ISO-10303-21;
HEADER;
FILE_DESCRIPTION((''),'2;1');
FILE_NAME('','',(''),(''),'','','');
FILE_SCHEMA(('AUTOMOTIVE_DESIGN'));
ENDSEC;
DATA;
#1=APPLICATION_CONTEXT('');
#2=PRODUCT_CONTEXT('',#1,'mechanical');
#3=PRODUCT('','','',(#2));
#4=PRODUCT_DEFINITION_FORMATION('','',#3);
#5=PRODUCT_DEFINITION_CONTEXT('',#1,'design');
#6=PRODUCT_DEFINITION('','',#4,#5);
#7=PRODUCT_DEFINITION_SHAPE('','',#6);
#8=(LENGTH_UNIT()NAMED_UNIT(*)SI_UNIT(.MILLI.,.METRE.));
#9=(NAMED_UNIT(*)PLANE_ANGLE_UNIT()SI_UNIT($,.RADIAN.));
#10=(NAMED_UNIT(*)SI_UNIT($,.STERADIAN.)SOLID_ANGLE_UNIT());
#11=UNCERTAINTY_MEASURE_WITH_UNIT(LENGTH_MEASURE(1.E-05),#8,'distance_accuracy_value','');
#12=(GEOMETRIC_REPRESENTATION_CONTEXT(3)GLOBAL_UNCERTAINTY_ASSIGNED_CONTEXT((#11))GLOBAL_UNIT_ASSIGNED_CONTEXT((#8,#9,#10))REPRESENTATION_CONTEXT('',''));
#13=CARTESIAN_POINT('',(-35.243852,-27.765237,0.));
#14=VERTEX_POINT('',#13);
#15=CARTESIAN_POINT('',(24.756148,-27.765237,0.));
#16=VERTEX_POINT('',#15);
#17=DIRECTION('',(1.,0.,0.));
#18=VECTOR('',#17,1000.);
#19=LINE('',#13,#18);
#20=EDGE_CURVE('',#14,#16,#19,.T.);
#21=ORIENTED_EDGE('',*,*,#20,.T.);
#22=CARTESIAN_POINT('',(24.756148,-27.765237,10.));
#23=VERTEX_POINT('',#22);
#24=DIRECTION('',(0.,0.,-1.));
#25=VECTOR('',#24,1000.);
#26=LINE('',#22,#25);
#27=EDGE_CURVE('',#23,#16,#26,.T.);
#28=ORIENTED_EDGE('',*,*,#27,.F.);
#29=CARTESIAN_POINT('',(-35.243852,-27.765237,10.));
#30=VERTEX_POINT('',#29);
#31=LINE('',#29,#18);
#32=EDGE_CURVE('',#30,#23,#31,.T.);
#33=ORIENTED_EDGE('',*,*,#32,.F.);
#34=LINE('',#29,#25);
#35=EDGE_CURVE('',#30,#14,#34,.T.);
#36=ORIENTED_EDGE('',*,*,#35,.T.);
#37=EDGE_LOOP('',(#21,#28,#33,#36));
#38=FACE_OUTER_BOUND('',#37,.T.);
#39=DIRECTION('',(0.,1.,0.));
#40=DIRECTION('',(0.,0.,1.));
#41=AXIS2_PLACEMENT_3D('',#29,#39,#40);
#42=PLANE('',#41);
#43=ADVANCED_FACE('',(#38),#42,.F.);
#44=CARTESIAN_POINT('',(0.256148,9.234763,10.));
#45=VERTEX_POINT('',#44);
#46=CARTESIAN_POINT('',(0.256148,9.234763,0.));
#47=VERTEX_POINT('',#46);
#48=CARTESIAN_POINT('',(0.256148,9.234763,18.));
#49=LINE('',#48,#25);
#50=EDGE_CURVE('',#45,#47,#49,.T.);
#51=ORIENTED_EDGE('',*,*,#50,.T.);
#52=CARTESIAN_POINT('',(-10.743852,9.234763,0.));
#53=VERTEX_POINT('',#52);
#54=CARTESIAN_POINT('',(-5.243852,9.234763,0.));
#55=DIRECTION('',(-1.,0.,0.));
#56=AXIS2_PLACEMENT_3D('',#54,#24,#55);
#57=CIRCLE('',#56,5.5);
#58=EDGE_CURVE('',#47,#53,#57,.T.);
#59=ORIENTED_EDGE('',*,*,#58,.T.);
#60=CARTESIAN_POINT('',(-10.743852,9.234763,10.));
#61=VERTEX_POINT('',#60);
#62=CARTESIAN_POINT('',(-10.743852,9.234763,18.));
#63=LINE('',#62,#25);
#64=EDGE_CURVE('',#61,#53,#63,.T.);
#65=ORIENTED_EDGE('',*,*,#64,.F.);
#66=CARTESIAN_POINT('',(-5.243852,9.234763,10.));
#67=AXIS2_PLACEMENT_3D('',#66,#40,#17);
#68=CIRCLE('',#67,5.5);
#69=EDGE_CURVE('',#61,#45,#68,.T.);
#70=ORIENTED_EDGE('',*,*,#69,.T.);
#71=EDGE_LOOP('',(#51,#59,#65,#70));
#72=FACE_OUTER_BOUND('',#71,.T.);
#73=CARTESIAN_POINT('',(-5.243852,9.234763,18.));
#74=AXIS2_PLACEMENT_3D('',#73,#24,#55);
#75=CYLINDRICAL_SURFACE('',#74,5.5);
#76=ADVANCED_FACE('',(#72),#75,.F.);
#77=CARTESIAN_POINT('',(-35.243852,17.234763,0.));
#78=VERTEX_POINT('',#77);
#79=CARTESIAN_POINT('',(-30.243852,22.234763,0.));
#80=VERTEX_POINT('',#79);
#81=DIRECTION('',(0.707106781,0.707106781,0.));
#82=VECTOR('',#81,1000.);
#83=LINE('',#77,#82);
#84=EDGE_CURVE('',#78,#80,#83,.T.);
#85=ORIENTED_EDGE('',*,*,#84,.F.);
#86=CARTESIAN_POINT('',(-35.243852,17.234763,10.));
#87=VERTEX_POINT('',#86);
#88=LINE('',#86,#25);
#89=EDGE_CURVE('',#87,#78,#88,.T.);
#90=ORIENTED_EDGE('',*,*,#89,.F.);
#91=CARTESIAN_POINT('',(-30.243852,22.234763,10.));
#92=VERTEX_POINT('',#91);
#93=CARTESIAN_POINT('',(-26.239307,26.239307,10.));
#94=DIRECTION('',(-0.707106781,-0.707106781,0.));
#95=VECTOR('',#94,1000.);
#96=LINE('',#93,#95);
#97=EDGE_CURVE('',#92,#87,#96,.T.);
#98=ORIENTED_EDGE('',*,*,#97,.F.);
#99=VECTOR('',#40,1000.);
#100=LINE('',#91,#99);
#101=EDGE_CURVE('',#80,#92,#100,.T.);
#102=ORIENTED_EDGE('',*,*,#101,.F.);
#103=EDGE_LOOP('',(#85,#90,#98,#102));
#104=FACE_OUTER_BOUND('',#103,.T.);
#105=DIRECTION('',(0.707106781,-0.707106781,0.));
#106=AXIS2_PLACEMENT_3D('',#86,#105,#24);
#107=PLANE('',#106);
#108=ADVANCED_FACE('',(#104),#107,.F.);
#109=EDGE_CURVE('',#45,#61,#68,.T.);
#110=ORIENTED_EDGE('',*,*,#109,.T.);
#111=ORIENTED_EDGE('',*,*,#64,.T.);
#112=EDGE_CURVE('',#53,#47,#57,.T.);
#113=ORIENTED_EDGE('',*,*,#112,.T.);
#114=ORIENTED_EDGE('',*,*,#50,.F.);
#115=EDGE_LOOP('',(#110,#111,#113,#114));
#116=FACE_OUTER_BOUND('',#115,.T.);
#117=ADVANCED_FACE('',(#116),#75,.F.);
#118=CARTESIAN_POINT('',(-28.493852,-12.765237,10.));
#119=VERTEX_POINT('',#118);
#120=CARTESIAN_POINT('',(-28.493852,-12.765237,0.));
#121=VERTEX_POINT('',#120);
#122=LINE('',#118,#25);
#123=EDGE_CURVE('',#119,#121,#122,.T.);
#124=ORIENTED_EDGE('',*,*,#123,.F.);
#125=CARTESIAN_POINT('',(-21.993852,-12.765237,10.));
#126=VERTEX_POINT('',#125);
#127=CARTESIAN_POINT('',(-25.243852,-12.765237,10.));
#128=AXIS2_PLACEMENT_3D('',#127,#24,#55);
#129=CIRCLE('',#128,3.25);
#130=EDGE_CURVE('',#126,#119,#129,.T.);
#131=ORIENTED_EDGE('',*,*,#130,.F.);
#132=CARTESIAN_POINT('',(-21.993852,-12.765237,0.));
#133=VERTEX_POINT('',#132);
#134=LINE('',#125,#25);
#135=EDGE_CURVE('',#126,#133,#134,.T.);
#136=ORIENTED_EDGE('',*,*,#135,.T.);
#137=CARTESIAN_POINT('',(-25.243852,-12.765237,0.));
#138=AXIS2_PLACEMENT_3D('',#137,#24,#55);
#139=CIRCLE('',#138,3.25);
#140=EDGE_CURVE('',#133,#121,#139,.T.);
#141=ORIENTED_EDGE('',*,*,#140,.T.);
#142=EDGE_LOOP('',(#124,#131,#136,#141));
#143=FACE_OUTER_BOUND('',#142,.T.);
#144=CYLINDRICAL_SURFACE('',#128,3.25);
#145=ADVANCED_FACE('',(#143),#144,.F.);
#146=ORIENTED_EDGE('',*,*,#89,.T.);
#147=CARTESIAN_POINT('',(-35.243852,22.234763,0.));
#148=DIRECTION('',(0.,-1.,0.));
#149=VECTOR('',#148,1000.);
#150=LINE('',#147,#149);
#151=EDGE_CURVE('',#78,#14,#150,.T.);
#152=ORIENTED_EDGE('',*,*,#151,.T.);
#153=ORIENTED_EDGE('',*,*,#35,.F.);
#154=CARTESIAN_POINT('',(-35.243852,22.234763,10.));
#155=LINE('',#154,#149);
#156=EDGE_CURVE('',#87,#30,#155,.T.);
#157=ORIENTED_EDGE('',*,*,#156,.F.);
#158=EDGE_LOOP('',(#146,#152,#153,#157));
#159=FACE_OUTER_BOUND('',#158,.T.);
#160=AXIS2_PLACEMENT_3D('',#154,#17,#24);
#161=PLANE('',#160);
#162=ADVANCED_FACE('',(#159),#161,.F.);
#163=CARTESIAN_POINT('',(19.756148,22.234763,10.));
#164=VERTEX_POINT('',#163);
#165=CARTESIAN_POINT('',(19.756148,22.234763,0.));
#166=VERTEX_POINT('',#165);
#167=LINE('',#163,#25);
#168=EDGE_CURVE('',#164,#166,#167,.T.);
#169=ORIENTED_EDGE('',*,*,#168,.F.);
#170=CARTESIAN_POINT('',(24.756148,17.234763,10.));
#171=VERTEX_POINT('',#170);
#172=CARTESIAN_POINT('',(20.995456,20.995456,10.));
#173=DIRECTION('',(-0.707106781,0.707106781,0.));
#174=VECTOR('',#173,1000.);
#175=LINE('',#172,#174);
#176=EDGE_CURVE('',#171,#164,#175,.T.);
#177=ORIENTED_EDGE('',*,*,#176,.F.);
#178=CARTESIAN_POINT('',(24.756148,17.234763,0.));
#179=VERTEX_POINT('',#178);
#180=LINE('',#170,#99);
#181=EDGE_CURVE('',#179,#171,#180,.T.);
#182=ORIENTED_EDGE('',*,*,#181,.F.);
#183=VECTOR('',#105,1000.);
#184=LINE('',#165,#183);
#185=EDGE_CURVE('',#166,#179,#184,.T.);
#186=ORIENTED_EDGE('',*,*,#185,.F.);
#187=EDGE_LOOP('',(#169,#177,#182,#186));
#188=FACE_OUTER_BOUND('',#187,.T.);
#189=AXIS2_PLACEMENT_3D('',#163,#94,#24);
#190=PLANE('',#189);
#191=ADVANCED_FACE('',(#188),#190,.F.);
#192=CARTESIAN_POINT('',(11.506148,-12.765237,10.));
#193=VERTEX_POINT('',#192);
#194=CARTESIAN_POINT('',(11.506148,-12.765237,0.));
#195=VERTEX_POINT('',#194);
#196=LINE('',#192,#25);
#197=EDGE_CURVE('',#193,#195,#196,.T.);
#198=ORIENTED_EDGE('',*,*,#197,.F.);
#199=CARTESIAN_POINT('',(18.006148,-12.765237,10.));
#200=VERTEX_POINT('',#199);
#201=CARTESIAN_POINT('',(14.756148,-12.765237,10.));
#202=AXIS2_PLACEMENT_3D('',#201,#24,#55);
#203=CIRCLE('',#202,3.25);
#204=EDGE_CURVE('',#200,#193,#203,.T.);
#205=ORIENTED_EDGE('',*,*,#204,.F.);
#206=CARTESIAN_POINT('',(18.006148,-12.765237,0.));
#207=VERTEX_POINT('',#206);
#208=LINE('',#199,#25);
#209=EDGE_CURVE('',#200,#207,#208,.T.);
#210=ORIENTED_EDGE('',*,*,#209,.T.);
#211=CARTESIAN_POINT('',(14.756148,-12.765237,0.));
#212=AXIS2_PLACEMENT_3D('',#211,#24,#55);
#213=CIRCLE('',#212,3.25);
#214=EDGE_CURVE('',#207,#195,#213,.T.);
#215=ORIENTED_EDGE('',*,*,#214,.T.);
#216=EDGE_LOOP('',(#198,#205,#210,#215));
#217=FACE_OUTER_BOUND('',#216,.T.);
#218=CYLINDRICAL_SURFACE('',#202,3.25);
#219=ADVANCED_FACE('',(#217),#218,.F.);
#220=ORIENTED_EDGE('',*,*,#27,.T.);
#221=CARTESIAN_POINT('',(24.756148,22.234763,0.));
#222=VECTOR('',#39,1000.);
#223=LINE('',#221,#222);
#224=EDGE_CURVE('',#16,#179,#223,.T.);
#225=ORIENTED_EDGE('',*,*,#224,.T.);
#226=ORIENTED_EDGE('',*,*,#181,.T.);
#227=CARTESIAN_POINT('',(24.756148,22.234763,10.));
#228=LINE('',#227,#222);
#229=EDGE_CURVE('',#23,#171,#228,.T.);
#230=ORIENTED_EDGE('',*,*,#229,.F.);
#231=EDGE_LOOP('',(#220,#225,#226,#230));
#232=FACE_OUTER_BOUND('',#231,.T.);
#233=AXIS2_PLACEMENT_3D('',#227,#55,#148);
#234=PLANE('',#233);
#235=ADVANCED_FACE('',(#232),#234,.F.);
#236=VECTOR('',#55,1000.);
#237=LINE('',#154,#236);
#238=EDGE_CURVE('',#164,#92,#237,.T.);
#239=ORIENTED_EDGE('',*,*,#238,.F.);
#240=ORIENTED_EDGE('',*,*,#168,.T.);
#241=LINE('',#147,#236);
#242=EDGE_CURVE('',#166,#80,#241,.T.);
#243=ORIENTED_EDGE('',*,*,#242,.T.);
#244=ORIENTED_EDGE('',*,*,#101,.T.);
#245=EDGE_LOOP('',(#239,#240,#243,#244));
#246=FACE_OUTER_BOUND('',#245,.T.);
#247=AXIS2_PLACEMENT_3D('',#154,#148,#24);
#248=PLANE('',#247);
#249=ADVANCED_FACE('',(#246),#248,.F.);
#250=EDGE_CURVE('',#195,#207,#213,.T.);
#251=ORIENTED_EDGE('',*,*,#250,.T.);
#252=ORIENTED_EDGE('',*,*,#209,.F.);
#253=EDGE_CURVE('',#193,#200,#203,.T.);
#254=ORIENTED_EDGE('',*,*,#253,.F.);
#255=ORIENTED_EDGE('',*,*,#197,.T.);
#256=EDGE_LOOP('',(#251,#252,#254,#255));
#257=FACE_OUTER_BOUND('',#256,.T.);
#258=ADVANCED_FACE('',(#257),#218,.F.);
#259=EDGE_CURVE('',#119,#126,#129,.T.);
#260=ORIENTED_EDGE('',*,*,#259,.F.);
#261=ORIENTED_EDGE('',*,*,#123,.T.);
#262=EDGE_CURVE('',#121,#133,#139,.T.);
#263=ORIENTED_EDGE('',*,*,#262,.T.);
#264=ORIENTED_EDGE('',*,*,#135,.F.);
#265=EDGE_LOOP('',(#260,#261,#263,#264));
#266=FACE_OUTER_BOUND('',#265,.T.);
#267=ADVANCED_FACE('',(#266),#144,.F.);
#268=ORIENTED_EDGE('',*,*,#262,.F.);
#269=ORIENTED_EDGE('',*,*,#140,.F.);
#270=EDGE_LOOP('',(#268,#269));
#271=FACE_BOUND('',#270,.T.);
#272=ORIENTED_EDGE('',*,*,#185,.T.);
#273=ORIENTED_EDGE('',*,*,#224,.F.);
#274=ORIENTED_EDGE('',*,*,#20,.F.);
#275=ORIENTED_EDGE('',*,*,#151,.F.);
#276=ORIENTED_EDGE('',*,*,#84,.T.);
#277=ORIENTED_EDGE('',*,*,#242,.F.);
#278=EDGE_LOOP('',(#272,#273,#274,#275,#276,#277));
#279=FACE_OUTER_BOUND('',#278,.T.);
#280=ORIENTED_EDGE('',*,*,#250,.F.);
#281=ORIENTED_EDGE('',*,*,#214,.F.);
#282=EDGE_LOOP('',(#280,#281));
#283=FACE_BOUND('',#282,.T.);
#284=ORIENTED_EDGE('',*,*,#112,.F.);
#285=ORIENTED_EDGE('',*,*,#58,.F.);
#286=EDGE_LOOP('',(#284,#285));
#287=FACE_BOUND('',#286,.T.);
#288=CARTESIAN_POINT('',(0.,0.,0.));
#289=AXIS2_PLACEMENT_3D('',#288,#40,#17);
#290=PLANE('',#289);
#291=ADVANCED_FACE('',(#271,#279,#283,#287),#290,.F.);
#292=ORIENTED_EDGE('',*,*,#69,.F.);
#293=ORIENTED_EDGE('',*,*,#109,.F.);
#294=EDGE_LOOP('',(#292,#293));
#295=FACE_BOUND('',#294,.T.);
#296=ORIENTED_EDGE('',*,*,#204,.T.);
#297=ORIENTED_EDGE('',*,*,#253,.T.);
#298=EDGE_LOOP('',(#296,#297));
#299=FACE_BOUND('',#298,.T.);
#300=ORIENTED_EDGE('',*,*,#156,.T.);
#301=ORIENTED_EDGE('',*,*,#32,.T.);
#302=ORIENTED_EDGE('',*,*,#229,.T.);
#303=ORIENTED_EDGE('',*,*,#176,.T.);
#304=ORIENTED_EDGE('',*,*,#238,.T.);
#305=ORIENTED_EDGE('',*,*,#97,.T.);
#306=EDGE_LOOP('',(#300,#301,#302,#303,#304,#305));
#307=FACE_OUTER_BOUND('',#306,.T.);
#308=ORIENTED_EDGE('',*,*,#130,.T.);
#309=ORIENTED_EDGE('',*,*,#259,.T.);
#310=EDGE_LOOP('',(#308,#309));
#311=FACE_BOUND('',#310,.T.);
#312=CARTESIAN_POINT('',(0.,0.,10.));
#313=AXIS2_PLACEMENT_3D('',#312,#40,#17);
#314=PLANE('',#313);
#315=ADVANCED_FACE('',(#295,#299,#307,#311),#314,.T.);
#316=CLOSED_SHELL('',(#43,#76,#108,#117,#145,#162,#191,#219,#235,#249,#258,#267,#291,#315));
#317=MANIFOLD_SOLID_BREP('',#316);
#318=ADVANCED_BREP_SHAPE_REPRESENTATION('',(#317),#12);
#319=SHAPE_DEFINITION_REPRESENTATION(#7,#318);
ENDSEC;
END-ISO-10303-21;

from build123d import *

# Parameters (mm, degrees)
SKETCH1_W           = 60
SKETCH1_H           = 50
BOSS_EXTRUDE1_DEPTH = 10
SKETCH2_R           = 5.5
CUT_EXTRUDE1_DEPTH  = 18
CHAMFER1_SIZE       = 5
SKETCH3_R           = 3.25
CUT_EXTRUDE2_DEPTH  = 46.967787324


with BuildPart() as part:
    # Sketch1 → Boss-Extrude1 (new body)
    with BuildSketch(Plane.XY):
        with Locations((-5.243851729, -2.76523702)):
            Rectangle(SKETCH1_W, SKETCH1_H)
    extrude(amount=BOSS_EXTRUDE1_DEPTH)

    # Sketch2 → Cut-Extrude1 (cut)
    with BuildSketch(Plane(origin=(0, 0, 0), x_dir=(-1, 0, 0), z_dir=(0, 0, -1))):
        with Locations((5.243851729, 9.23476298)):
            Circle(SKETCH2_R)
    extrude(amount=-CUT_EXTRUDE1_DEPTH, mode=Mode.SUBTRACT)

    # Chamfer1
    chamfer1_edges = [part.edges().sort_by_distance(p)[0] for p in [
        (-35.243851729, 22.23476298, 5),
        (24.756148271, 22.23476298, 5),
    ]]
    chamfer(chamfer1_edges, length=CHAMFER1_SIZE)

    # Sketch3 → Cut-Extrude2 (cut, through all)
    with BuildSketch(Plane(origin=(0, 0, 0), x_dir=(-1, 0, 0), z_dir=(0, 0, -1))):
        with Locations((-14.756148271, -12.76523702)):
            Circle(SKETCH3_R)
        with Locations((25.243851729, -12.76523702)):
            Circle(SKETCH3_R)
    extrude(amount=-CUT_EXTRUDE2_DEPTH, mode=Mode.SUBTRACT)


solid = part.part
